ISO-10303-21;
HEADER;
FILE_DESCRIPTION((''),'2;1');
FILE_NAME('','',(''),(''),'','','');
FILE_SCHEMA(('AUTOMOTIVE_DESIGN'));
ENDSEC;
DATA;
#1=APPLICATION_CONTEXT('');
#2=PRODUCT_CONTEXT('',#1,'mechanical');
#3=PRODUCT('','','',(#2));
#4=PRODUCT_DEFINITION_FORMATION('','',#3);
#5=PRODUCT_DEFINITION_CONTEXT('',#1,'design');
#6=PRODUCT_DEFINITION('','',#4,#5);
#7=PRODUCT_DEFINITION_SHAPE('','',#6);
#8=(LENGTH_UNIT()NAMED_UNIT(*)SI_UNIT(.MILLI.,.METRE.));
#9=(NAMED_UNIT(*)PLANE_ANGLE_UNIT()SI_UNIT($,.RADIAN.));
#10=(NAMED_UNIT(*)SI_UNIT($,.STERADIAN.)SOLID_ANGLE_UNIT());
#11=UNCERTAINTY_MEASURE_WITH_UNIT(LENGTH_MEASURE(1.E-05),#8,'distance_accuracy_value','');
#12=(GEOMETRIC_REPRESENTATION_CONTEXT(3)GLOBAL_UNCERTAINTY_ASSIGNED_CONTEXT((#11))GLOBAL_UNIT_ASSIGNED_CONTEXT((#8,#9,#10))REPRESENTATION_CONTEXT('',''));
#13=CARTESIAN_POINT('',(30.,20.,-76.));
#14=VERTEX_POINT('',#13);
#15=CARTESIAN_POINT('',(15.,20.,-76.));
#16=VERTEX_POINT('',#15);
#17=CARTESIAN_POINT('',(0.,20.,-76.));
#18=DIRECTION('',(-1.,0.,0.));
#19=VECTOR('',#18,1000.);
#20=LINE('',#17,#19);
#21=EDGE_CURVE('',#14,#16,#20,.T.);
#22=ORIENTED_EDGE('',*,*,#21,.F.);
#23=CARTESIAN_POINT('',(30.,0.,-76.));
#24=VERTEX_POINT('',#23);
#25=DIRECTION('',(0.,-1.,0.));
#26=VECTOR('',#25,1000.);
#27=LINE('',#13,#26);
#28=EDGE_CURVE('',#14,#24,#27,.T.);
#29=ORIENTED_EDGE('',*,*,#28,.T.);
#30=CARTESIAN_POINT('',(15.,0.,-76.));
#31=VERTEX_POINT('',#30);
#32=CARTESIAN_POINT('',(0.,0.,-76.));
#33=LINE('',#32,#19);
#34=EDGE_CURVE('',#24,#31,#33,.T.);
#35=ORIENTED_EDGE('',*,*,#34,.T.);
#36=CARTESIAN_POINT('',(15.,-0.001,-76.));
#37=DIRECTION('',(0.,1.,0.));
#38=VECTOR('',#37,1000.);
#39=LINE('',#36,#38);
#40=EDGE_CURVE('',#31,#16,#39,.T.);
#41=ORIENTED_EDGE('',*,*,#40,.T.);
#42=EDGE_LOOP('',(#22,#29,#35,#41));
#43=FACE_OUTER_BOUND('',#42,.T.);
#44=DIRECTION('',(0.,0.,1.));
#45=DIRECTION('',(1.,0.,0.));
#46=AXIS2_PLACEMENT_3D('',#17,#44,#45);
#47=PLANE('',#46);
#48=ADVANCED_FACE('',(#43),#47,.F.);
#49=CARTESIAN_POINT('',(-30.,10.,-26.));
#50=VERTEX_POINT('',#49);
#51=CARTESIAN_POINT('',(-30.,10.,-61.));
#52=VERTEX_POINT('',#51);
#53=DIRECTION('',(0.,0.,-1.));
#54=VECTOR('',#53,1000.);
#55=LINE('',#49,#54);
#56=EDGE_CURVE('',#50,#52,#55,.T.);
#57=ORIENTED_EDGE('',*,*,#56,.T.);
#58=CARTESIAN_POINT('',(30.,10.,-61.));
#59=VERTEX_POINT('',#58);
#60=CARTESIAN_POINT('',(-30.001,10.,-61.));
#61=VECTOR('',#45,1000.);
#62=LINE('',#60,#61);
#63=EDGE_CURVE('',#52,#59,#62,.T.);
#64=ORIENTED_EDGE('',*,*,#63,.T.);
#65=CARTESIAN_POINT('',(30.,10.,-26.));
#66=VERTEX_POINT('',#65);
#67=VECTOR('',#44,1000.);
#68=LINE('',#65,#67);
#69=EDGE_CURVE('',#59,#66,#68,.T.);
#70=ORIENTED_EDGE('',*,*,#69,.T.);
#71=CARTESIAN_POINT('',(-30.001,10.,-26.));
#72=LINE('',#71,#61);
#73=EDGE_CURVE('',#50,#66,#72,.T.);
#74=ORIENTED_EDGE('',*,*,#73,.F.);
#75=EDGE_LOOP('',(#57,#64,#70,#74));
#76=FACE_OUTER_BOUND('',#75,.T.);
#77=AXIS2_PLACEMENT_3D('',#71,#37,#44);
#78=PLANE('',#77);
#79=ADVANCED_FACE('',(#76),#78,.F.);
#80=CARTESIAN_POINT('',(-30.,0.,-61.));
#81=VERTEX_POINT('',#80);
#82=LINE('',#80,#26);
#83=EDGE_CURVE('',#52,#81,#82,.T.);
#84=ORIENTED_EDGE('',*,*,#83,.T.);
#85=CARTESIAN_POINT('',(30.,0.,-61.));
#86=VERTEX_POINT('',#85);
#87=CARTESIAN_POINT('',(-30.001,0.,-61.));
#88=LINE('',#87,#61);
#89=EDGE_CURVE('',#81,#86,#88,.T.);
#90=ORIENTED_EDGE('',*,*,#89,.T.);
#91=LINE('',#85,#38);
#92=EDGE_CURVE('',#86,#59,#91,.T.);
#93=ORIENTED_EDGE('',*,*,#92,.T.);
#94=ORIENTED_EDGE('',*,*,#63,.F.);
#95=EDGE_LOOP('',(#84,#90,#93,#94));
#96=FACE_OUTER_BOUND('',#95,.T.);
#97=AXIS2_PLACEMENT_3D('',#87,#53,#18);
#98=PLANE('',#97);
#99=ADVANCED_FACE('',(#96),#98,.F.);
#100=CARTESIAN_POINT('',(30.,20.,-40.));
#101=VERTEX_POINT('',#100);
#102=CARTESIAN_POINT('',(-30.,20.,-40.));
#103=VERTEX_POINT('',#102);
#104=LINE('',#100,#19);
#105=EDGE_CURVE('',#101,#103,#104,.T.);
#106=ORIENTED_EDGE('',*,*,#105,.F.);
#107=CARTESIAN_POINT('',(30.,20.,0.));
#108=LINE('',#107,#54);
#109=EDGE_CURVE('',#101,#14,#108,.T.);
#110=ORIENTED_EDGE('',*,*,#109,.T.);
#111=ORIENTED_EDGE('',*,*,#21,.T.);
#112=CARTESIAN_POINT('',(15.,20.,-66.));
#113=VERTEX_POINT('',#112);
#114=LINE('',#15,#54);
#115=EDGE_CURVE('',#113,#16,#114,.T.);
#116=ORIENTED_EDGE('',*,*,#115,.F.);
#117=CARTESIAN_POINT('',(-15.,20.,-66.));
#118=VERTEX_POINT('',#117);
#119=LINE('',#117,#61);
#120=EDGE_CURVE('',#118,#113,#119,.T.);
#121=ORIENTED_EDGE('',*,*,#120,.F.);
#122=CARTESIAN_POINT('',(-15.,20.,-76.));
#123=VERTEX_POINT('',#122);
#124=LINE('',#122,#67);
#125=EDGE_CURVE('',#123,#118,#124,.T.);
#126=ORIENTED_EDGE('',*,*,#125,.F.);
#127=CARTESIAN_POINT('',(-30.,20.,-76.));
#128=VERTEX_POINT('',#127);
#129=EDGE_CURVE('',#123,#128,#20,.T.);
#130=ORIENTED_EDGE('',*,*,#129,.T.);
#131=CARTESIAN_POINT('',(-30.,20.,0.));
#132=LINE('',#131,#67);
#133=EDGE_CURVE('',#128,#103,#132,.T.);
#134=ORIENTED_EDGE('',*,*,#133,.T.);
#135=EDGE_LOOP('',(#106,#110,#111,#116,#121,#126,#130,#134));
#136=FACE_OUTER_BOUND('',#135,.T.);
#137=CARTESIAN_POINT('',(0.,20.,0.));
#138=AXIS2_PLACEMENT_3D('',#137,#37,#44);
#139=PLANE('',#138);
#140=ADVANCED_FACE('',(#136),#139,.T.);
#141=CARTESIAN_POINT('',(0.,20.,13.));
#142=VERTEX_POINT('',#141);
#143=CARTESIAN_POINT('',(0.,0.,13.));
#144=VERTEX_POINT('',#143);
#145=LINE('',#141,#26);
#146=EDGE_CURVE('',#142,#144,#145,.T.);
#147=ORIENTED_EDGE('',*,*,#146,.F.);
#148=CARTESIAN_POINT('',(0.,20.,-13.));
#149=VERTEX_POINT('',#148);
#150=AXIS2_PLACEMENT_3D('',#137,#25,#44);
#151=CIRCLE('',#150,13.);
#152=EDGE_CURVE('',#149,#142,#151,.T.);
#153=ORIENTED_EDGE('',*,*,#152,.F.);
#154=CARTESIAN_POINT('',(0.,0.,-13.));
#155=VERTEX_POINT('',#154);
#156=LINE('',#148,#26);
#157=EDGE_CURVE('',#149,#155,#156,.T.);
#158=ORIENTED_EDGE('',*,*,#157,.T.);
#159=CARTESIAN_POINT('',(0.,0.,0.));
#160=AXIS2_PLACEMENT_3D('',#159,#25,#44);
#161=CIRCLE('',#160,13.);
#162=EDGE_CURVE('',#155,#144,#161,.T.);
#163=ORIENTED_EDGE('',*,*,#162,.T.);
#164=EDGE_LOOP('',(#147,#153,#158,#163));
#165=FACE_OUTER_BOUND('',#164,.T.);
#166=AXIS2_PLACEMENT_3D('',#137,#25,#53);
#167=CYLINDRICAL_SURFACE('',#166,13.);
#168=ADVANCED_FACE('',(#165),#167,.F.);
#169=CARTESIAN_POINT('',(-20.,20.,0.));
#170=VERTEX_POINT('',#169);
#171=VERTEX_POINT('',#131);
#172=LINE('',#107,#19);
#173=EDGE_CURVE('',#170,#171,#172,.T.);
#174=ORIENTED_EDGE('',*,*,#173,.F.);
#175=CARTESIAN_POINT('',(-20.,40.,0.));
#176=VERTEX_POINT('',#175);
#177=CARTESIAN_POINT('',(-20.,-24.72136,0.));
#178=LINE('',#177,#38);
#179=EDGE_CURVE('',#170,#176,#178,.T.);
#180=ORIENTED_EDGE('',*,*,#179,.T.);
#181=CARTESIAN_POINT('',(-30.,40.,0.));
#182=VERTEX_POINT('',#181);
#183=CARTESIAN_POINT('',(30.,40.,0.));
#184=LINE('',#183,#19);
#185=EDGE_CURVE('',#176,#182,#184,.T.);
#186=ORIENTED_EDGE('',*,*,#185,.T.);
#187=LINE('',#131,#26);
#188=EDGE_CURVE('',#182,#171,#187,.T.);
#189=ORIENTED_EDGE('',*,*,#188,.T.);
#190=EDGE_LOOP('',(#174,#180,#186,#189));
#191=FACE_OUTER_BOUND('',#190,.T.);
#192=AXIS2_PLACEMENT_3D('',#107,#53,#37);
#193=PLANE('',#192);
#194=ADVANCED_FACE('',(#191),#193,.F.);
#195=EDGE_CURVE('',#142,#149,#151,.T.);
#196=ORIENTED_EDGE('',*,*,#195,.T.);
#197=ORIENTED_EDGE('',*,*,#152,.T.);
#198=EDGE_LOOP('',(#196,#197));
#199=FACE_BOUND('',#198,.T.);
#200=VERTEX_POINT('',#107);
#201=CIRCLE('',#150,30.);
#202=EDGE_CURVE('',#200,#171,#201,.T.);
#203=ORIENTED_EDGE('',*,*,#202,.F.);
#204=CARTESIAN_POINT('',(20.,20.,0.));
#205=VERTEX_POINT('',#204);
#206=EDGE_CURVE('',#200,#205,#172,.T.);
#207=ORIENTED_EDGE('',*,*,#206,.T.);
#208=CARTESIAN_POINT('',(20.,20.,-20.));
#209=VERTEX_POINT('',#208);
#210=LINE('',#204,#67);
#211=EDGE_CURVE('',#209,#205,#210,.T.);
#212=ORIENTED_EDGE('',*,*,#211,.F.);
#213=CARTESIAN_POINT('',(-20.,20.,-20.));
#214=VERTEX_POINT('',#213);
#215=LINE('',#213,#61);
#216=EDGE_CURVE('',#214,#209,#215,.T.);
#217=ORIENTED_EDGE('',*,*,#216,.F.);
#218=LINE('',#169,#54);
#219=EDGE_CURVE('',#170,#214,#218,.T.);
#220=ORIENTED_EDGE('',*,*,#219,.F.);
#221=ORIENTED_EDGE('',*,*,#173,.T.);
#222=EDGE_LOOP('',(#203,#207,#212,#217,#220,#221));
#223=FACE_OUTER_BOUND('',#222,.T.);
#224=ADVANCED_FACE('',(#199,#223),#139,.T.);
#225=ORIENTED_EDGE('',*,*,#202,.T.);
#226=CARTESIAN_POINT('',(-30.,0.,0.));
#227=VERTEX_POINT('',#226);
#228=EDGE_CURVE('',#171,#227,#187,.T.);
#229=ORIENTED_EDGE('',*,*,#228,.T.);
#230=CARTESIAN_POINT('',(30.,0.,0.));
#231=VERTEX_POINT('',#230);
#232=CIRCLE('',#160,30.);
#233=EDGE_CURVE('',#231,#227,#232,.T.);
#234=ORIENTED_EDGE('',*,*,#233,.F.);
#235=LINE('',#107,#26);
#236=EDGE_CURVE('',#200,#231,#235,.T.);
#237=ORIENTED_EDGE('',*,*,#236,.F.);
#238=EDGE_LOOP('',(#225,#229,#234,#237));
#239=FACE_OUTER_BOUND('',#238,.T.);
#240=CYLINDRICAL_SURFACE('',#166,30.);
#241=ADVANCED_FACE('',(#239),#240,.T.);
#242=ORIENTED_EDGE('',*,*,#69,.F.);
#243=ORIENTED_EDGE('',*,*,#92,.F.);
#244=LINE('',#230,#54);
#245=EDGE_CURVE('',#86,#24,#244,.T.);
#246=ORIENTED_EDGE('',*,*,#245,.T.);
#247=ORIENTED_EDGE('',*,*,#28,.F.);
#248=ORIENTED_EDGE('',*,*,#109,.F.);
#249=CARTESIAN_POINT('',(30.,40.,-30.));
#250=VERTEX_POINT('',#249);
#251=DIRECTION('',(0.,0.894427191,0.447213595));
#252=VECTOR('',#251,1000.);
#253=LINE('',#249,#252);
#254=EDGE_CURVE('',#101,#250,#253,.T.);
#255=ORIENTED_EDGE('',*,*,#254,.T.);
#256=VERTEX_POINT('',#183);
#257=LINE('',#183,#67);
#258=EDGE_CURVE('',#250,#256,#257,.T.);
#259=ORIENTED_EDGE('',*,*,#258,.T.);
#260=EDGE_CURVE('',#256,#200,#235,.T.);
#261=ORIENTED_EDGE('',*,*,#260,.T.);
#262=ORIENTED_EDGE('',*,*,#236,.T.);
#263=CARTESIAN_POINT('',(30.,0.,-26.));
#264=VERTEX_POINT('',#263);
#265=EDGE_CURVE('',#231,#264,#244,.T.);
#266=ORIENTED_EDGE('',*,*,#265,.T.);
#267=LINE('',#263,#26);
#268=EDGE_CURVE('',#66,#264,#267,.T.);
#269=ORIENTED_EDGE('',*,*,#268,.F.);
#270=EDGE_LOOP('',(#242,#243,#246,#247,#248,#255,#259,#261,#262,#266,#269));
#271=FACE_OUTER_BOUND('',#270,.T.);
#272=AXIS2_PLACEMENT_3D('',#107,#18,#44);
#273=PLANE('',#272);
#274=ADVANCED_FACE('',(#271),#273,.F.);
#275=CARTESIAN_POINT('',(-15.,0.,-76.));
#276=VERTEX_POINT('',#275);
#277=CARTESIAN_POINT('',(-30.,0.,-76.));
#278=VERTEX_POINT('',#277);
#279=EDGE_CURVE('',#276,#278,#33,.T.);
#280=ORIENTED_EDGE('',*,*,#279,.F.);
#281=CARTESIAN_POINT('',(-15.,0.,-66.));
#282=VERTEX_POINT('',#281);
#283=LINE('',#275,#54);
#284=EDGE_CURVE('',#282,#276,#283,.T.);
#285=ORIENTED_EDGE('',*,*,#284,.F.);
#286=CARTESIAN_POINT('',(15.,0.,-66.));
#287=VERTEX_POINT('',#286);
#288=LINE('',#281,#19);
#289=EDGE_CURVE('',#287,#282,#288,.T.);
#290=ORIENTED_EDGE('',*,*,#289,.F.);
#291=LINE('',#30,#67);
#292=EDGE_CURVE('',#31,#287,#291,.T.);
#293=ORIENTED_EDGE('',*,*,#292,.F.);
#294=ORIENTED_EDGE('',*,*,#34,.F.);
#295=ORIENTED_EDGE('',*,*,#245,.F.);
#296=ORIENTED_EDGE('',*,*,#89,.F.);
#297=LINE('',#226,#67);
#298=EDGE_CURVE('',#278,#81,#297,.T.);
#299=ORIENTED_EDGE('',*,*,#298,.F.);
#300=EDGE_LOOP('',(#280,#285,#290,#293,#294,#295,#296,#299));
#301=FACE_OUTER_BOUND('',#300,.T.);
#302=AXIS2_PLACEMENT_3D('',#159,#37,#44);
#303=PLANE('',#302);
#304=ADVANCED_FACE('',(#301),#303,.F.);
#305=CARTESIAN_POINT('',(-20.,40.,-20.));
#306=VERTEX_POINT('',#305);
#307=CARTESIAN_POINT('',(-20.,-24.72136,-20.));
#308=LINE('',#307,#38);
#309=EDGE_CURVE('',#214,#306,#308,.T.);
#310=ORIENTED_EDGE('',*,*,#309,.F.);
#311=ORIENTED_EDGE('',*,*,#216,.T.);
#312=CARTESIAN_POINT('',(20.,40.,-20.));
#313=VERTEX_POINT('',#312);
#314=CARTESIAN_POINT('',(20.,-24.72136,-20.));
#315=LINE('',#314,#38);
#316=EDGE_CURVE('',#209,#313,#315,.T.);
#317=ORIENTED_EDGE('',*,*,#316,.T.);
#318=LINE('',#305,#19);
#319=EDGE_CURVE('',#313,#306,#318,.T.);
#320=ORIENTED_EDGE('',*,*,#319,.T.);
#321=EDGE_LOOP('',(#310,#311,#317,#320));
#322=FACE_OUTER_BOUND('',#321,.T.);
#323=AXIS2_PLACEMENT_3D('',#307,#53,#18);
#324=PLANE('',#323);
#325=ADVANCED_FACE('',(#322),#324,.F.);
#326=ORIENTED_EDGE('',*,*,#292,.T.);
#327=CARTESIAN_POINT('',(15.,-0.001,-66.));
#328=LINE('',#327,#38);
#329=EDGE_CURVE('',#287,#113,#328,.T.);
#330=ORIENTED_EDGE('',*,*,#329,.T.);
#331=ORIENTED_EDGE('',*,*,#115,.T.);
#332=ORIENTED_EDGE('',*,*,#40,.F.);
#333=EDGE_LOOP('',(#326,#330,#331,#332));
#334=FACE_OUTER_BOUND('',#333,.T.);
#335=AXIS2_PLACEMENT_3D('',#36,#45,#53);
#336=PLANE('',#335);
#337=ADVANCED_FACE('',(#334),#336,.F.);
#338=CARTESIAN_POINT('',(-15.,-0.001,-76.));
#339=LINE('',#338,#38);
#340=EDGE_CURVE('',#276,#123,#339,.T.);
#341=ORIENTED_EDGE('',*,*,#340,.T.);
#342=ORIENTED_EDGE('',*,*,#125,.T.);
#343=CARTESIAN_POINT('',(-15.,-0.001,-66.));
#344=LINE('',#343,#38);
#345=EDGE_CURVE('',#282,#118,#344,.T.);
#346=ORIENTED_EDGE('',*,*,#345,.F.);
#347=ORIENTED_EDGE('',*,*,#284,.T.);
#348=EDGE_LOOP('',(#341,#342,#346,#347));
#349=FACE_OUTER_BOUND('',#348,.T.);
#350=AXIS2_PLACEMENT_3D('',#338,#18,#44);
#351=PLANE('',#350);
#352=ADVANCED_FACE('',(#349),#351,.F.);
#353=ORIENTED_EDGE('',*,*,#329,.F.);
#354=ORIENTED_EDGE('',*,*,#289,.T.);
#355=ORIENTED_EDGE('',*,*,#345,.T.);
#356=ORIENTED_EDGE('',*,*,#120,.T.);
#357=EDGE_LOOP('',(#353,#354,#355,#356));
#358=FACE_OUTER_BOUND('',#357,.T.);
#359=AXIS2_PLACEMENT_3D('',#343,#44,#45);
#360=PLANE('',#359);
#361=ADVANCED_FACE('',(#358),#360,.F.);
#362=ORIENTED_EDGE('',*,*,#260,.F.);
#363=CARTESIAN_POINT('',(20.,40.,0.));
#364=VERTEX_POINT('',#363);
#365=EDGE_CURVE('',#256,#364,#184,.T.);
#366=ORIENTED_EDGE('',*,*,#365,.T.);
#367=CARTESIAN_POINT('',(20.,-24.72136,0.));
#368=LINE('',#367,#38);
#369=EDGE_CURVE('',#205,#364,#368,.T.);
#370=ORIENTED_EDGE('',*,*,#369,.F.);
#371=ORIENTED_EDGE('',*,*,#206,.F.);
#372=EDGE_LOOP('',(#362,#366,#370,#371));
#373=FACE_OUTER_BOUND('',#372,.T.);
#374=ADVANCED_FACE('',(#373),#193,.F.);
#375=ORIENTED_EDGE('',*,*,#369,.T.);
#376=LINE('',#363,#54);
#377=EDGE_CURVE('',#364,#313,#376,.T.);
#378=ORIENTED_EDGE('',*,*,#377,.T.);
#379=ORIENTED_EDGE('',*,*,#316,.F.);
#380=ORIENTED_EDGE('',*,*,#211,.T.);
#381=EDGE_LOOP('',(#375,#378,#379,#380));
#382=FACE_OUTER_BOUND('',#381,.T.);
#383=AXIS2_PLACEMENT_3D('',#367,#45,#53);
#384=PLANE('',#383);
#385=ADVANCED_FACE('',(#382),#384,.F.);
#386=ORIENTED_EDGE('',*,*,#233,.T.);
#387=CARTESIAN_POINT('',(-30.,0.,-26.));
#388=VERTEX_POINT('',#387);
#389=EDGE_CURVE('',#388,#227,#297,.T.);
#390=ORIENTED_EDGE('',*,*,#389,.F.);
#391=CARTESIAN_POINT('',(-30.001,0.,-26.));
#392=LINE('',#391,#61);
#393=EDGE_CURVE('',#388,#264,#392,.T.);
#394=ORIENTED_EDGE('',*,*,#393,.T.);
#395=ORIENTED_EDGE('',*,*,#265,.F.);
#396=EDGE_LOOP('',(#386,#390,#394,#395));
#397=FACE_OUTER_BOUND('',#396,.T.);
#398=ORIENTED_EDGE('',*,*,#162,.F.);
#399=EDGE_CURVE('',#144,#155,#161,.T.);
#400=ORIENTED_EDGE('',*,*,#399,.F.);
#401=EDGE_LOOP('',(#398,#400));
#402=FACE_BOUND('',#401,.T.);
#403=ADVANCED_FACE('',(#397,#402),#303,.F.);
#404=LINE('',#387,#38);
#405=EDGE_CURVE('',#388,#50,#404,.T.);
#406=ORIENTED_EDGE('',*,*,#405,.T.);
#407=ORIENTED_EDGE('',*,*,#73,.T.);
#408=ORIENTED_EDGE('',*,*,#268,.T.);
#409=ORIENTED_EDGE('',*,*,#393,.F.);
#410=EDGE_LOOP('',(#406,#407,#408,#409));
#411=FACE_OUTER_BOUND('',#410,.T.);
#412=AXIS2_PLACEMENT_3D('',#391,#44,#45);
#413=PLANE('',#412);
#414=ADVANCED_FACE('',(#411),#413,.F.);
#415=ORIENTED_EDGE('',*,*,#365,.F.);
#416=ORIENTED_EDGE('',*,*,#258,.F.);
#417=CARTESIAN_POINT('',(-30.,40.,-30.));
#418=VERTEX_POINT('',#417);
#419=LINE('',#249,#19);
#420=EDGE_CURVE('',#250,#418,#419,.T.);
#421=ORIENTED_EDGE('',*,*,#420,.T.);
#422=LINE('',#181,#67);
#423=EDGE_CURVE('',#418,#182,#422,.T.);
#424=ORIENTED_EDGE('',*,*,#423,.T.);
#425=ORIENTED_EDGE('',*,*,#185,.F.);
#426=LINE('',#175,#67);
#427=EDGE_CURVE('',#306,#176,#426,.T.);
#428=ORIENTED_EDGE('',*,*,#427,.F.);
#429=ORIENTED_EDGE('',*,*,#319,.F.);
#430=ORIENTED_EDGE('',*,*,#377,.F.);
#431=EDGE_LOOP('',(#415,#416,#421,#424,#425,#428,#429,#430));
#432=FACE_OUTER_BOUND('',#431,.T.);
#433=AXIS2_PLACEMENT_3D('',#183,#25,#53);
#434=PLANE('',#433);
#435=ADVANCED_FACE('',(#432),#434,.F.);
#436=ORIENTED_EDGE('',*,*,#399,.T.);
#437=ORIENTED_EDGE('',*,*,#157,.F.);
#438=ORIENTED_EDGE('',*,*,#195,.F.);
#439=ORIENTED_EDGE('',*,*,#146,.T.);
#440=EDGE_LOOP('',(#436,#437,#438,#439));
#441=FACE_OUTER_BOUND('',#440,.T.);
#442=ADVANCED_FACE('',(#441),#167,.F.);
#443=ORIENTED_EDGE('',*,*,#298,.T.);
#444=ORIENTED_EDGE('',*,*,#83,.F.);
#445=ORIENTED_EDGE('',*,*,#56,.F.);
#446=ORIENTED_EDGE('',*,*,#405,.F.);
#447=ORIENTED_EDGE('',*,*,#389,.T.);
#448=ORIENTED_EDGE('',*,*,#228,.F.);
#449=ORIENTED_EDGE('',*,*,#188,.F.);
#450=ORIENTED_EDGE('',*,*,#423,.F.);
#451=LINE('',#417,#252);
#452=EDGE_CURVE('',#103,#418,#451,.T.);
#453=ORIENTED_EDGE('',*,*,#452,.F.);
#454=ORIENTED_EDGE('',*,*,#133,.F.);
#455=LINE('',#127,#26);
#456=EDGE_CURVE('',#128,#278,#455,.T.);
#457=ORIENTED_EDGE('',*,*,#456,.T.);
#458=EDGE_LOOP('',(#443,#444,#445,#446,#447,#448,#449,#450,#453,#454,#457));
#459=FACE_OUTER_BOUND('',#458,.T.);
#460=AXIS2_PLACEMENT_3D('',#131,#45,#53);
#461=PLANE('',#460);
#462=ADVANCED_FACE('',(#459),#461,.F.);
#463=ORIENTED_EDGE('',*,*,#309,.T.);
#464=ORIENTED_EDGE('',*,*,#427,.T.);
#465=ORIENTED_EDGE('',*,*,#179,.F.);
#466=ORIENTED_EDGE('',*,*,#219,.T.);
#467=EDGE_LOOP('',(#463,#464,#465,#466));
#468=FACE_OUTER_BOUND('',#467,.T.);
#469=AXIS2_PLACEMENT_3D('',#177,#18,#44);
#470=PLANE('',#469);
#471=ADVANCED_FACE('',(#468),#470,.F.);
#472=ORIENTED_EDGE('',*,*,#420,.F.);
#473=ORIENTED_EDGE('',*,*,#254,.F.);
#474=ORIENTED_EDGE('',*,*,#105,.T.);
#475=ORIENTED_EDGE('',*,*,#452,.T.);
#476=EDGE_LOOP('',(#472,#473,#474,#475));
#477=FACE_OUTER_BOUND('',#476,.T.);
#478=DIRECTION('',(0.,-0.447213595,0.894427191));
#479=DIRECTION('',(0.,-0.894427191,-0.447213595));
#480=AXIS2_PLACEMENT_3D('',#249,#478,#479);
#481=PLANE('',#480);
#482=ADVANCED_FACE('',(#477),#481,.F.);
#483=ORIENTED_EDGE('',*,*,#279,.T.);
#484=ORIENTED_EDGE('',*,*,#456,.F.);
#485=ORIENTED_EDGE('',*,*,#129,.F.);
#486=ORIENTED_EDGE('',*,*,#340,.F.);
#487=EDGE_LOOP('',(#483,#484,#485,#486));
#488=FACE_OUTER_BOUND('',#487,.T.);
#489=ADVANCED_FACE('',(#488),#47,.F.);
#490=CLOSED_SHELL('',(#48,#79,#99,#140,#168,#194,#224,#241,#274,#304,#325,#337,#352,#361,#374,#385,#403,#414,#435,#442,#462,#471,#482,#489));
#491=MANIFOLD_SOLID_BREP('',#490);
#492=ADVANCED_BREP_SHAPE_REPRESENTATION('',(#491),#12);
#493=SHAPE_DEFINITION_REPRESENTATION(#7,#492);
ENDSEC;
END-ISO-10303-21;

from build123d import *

# Parameters (mm, degrees)
BASE_PLATE_PROFILE_SKETCH_R   = 30
BASE_PLATE_PROFILE_SKETCH_R_2 = 13
BASE_PLATE_DEPTH              = 20
BASE_SLOT_CUT_REACH           = 100.874
BASE_SLOT_SKETCH_W            = 35
BASE_SLOT_SKETCH_H            = 10
BORE_CUT_REACH                = 86.119
BORE_SKETCH_W                 = 30
BORE_SKETCH_H                 = 10
UPRIGHT_BLOCK_DEPTH           = 30
UPRIGHT_BLOCK_DEPTH_BACK      = 30
UPRIGHT_POCKET_SKETCH_W       = 40
UPRIGHT_POCKET_SKETCH_H       = 20
UPRIGHT_POCKET_CUT_DEPTH      = 20


with BuildPart() as part:
    # Base Plate Profile Sketch → Base Plate (new body)
    # profile 1 of 2: a face of its own
    with BuildSketch(Plane(origin=(0, 0, 0), x_dir=(0, 0, -1), z_dir=(0, -1, 0))):
        with BuildLine():
            Line((76, 30), (0, 30))
            ThreePointArc((0, 30), (21.213203436, 21.213203436), (30, 0))
            ThreePointArc((30, 0), (21.213203436, -21.213203436), (0, -30))
            Line((0, -30), (76, -30))
            Line((76, -30), (76, 30))
        make_face()
    # profile 2 of 2: a face of its own
    with BuildSketch(Plane(origin=(0, 0, 0), x_dir=(0, 0, -1), z_dir=(0, -1, 0))):
        Circle(BASE_PLATE_PROFILE_SKETCH_R)
        with Locations(Location((0, 0, 0), (0, 0, 180))):
            Circle(BASE_PLATE_PROFILE_SKETCH_R_2, mode=Mode.SUBTRACT)
    extrude(amount=-BASE_PLATE_DEPTH)

    # Base Slot Sketch → Base Slot Cut (cut, up to next)
    with BuildSketch(Plane(origin=(30, 0, 0), x_dir=(0, 0, -1), z_dir=(1, 0, 0)), mode=Mode.PRIVATE) as base_slot_cut_sk1:
        with Locations((43.5, 5)):
            Rectangle(BASE_SLOT_SKETCH_W, BASE_SLOT_SKETCH_H)
    base_slot_cut_tool1 = extrude(base_slot_cut_sk1.sketch, amount=-BASE_SLOT_CUT_REACH, mode=Mode.PRIVATE) & part.part
    add(base_slot_cut_tool1.solids().sort_by_distance((30, 5, -43.5))[0], mode=Mode.SUBTRACT)

    # Bore Sketch → Bore Cut (cut, up to next)
    with BuildSketch(Plane(origin=(0, 20, 0), x_dir=(1, 0, 0), z_dir=(0, 1, 0)), mode=Mode.PRIVATE) as bore_cut_sk1:
        with Locations((0, 71)):
            Rectangle(BORE_SKETCH_W, BORE_SKETCH_H)
    bore_cut_tool1 = extrude(bore_cut_sk1.sketch, amount=-BORE_CUT_REACH, mode=Mode.PRIVATE) & part.part
    add(bore_cut_tool1.solids().sort_by_distance((0, 20, -71))[0], mode=Mode.SUBTRACT)

    # Upright Block Profile Sketch → Upright Block (add, two sides: drawn at the far end of the back side and taken through both)
    with BuildSketch(Plane(origin=(0, 0, 0), x_dir=(0, 0, -1), z_dir=(1, 0, 0)).offset(-UPRIGHT_BLOCK_DEPTH_BACK)):
        Polygon((0, 20), (0, 40), (30, 40), (40, 20), align=None)
    extrude(amount=UPRIGHT_BLOCK_DEPTH + UPRIGHT_BLOCK_DEPTH_BACK)

    # Upright Pocket Sketch → Upright Pocket Cut (cut)
    with BuildSketch(Plane(origin=(0, 40, 0), x_dir=(1, 0, 0), z_dir=(0, 1, 0))):
        with Locations((0, 10)):
            Rectangle(UPRIGHT_POCKET_SKETCH_W, UPRIGHT_POCKET_SKETCH_H)
    extrude(amount=-UPRIGHT_POCKET_CUT_DEPTH, mode=Mode.SUBTRACT)


solid = part.part
